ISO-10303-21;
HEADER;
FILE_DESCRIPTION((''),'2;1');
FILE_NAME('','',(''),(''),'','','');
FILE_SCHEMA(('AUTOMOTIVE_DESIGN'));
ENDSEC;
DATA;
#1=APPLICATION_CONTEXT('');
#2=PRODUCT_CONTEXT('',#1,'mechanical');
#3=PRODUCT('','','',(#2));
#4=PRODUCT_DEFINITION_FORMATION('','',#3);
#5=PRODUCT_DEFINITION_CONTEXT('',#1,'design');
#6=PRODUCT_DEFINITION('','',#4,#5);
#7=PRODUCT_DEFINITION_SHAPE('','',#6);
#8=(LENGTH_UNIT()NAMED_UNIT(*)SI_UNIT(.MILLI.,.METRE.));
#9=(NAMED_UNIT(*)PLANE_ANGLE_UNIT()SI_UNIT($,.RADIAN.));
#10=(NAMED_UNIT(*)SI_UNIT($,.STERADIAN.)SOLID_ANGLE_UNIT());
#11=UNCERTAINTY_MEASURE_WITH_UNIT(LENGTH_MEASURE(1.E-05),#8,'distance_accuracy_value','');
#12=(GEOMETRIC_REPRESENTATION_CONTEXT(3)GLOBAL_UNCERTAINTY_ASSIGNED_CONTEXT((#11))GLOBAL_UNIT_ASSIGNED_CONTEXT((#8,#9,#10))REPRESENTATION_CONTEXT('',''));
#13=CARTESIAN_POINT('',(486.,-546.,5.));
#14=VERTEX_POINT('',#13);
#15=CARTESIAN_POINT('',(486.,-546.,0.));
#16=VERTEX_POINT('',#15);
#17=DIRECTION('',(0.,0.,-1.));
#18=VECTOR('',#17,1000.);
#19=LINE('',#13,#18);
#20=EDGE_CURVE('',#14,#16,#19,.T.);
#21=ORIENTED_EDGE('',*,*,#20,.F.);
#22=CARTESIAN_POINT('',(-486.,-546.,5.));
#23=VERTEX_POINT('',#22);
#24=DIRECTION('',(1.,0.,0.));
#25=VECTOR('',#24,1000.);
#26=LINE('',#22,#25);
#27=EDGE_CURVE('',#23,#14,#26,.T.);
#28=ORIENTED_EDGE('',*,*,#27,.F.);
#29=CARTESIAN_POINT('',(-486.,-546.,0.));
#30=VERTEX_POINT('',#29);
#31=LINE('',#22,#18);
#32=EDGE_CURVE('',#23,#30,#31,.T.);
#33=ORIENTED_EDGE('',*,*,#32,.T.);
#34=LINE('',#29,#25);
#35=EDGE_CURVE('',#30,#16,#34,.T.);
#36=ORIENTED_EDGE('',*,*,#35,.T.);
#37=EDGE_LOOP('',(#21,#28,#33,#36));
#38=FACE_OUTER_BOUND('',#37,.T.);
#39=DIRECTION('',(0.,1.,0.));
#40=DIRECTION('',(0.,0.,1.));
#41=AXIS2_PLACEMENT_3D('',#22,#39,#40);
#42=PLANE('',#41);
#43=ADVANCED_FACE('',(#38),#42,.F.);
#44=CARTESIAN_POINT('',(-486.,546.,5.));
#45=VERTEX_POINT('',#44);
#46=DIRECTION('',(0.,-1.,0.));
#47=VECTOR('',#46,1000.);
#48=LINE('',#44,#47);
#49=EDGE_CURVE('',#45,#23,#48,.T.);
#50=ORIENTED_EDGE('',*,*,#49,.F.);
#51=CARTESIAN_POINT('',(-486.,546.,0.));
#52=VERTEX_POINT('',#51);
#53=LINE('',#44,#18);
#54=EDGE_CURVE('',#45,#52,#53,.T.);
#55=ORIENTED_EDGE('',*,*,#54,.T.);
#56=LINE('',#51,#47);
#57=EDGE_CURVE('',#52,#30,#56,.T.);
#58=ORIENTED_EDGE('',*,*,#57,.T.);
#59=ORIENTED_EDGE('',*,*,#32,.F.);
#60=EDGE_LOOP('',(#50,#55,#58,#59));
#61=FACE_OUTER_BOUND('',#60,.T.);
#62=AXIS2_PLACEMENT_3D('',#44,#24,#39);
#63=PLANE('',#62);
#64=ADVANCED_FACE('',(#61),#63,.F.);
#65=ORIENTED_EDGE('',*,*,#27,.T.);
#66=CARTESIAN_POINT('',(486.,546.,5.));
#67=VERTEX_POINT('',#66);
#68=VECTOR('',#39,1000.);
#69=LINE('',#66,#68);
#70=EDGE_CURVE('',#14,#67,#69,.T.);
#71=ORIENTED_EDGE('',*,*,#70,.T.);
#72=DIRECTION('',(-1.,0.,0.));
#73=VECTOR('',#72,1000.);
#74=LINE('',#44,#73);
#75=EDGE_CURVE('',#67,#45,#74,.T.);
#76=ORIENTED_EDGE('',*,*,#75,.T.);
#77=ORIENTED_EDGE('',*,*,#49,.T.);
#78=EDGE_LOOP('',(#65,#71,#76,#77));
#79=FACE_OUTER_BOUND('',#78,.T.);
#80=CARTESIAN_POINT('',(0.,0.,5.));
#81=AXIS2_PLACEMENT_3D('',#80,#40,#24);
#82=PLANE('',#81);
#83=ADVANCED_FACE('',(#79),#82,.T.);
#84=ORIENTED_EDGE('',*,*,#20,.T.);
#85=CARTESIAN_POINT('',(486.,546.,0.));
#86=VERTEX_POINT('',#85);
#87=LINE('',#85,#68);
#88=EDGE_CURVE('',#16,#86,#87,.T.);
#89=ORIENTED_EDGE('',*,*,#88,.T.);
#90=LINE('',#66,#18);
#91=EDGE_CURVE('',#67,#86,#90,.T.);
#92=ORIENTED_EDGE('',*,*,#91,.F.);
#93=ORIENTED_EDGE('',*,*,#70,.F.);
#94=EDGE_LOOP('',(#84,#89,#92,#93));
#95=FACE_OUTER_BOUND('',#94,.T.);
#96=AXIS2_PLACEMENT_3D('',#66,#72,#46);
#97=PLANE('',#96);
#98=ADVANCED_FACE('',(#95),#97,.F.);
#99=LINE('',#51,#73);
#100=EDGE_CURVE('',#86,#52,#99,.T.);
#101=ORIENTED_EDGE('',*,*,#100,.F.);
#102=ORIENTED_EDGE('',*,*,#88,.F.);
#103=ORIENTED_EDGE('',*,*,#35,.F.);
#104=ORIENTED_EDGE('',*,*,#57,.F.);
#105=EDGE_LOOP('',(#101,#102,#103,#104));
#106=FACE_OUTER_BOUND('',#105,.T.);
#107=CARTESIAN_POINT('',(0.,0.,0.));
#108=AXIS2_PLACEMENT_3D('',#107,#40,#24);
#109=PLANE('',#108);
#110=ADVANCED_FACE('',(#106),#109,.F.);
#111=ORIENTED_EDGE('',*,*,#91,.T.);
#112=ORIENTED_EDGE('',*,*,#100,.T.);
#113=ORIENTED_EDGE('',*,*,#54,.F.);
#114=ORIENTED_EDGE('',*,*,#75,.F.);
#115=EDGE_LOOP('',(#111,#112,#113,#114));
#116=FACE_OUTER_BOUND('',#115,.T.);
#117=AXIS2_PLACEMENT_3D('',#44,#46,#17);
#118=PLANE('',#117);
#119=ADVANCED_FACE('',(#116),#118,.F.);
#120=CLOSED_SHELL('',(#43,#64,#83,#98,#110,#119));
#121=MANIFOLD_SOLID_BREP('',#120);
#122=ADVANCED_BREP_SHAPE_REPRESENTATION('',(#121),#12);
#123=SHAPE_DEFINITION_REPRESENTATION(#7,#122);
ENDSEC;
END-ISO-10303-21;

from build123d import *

# Parameters (mm, degrees)
SKETCH_1_W      = 972
SKETCH_1_H      = 1092
EXTRUDE_1_DEPTH = 5


with BuildPart() as part:
    # 草图1 → 凸台-拉伸1 (new body)
    with BuildSketch(Plane.XY):
        Rectangle(SKETCH_1_W, SKETCH_1_H)
    extrude(amount=EXTRUDE_1_DEPTH)


solid = part.part
